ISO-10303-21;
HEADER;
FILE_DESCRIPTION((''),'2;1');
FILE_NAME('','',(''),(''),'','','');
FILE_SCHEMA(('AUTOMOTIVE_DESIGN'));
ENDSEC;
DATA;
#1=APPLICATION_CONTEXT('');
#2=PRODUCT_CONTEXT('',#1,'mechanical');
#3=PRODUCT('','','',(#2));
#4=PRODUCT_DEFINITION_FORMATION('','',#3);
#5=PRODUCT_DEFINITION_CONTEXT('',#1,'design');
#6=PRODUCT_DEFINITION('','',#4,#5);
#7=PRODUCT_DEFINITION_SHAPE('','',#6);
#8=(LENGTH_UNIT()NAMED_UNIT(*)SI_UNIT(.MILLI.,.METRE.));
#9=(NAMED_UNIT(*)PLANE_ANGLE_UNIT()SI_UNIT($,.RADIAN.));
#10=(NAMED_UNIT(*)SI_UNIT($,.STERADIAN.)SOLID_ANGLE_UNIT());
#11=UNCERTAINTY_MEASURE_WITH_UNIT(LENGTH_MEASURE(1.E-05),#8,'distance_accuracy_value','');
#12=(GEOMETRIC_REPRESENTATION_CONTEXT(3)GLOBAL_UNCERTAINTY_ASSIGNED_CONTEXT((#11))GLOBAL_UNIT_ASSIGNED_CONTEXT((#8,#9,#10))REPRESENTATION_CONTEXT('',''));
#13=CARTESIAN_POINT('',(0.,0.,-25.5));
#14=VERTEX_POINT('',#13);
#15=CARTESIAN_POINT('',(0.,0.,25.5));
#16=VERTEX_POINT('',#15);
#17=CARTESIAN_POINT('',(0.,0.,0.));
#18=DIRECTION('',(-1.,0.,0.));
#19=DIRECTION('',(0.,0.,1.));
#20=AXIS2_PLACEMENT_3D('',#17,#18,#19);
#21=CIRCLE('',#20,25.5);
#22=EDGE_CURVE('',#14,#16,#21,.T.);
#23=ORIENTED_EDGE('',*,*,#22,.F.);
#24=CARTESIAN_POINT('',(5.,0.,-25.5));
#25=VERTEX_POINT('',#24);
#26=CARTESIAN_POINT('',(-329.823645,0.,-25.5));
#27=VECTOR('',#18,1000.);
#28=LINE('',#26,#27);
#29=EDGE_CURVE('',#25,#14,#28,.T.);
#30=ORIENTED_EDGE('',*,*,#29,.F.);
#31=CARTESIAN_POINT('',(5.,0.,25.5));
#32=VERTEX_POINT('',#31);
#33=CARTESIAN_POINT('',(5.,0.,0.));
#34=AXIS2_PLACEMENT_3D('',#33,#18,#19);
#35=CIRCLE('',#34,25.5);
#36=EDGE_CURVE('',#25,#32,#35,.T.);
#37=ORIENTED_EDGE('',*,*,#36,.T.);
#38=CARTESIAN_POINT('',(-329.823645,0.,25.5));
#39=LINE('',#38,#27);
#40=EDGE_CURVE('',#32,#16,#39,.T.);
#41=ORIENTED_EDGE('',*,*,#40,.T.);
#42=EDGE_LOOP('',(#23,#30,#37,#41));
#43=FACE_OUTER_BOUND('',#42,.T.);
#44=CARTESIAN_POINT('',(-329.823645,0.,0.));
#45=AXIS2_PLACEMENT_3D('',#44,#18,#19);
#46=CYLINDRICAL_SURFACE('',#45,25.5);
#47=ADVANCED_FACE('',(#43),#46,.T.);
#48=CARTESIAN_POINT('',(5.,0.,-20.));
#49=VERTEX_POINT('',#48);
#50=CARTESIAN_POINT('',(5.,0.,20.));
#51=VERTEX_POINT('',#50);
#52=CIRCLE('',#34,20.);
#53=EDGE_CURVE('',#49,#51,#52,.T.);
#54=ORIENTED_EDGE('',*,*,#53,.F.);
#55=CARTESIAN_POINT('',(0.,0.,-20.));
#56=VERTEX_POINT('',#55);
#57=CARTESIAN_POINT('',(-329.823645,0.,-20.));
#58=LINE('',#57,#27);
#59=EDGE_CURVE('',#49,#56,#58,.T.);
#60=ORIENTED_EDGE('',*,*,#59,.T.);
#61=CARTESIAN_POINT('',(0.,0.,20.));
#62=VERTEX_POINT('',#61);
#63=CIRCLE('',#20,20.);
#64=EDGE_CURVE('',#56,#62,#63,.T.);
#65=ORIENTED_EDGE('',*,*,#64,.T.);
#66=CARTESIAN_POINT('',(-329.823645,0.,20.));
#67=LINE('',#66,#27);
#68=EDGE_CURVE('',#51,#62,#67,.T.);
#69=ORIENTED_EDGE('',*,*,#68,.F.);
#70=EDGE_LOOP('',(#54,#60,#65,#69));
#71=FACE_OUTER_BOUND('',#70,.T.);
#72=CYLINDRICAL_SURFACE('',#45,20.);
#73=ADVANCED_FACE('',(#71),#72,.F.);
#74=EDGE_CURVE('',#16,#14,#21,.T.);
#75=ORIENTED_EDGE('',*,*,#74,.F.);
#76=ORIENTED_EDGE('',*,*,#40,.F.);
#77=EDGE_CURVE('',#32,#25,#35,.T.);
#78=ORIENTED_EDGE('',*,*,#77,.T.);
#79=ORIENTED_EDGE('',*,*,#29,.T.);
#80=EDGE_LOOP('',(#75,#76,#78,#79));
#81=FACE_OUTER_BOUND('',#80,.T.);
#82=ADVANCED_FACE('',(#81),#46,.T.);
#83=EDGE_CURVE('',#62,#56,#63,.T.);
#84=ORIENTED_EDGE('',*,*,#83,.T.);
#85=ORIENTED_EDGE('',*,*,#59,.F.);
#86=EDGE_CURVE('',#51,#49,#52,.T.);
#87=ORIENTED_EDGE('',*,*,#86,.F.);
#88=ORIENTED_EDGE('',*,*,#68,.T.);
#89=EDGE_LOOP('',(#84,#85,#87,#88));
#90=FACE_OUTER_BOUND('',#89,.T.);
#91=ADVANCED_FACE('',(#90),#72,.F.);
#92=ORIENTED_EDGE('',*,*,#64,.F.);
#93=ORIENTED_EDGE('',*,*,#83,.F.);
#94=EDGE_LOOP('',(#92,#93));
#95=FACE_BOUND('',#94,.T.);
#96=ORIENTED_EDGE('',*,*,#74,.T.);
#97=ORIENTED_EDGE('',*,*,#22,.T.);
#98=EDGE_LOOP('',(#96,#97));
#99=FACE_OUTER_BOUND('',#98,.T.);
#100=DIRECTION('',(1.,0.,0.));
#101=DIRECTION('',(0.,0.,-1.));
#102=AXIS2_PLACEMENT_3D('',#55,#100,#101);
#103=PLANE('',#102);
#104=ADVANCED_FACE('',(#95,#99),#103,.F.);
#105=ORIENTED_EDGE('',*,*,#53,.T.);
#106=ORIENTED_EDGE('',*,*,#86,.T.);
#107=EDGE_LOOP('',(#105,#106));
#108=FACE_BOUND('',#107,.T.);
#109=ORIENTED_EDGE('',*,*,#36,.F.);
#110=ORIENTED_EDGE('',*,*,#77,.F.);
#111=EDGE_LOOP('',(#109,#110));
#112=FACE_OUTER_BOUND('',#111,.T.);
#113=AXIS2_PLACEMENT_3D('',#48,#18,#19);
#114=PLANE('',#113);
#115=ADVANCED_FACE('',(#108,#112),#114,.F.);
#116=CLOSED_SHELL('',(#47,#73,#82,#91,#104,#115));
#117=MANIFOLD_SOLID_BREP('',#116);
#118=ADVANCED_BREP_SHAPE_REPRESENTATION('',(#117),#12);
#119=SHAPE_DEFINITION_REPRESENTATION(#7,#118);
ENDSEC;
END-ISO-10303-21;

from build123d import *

# Parameters (mm, degrees)
SKETCH_1_W = 5
SKETCH_1_H = 5.5


with BuildPart() as part:
    # 草图1 → 旋转1 (revolve)
    with BuildSketch(Plane(origin=(0, 0, 0), x_dir=(1, 0, 0), z_dir=(0, 1, 0)), mode=Mode.PRIVATE) as revolve_1_sk:
        with Locations((2.5, 22.75)):
            Rectangle(SKETCH_1_W, SKETCH_1_H)
    revolve(revolve_1_sk.sketch.rotate(Axis((-329.823645462, 0, 0), (1, 0, 0)), 180), axis=Axis((-329.823645462, 0, 0), (1, 0, 0)))


solid = part.part
